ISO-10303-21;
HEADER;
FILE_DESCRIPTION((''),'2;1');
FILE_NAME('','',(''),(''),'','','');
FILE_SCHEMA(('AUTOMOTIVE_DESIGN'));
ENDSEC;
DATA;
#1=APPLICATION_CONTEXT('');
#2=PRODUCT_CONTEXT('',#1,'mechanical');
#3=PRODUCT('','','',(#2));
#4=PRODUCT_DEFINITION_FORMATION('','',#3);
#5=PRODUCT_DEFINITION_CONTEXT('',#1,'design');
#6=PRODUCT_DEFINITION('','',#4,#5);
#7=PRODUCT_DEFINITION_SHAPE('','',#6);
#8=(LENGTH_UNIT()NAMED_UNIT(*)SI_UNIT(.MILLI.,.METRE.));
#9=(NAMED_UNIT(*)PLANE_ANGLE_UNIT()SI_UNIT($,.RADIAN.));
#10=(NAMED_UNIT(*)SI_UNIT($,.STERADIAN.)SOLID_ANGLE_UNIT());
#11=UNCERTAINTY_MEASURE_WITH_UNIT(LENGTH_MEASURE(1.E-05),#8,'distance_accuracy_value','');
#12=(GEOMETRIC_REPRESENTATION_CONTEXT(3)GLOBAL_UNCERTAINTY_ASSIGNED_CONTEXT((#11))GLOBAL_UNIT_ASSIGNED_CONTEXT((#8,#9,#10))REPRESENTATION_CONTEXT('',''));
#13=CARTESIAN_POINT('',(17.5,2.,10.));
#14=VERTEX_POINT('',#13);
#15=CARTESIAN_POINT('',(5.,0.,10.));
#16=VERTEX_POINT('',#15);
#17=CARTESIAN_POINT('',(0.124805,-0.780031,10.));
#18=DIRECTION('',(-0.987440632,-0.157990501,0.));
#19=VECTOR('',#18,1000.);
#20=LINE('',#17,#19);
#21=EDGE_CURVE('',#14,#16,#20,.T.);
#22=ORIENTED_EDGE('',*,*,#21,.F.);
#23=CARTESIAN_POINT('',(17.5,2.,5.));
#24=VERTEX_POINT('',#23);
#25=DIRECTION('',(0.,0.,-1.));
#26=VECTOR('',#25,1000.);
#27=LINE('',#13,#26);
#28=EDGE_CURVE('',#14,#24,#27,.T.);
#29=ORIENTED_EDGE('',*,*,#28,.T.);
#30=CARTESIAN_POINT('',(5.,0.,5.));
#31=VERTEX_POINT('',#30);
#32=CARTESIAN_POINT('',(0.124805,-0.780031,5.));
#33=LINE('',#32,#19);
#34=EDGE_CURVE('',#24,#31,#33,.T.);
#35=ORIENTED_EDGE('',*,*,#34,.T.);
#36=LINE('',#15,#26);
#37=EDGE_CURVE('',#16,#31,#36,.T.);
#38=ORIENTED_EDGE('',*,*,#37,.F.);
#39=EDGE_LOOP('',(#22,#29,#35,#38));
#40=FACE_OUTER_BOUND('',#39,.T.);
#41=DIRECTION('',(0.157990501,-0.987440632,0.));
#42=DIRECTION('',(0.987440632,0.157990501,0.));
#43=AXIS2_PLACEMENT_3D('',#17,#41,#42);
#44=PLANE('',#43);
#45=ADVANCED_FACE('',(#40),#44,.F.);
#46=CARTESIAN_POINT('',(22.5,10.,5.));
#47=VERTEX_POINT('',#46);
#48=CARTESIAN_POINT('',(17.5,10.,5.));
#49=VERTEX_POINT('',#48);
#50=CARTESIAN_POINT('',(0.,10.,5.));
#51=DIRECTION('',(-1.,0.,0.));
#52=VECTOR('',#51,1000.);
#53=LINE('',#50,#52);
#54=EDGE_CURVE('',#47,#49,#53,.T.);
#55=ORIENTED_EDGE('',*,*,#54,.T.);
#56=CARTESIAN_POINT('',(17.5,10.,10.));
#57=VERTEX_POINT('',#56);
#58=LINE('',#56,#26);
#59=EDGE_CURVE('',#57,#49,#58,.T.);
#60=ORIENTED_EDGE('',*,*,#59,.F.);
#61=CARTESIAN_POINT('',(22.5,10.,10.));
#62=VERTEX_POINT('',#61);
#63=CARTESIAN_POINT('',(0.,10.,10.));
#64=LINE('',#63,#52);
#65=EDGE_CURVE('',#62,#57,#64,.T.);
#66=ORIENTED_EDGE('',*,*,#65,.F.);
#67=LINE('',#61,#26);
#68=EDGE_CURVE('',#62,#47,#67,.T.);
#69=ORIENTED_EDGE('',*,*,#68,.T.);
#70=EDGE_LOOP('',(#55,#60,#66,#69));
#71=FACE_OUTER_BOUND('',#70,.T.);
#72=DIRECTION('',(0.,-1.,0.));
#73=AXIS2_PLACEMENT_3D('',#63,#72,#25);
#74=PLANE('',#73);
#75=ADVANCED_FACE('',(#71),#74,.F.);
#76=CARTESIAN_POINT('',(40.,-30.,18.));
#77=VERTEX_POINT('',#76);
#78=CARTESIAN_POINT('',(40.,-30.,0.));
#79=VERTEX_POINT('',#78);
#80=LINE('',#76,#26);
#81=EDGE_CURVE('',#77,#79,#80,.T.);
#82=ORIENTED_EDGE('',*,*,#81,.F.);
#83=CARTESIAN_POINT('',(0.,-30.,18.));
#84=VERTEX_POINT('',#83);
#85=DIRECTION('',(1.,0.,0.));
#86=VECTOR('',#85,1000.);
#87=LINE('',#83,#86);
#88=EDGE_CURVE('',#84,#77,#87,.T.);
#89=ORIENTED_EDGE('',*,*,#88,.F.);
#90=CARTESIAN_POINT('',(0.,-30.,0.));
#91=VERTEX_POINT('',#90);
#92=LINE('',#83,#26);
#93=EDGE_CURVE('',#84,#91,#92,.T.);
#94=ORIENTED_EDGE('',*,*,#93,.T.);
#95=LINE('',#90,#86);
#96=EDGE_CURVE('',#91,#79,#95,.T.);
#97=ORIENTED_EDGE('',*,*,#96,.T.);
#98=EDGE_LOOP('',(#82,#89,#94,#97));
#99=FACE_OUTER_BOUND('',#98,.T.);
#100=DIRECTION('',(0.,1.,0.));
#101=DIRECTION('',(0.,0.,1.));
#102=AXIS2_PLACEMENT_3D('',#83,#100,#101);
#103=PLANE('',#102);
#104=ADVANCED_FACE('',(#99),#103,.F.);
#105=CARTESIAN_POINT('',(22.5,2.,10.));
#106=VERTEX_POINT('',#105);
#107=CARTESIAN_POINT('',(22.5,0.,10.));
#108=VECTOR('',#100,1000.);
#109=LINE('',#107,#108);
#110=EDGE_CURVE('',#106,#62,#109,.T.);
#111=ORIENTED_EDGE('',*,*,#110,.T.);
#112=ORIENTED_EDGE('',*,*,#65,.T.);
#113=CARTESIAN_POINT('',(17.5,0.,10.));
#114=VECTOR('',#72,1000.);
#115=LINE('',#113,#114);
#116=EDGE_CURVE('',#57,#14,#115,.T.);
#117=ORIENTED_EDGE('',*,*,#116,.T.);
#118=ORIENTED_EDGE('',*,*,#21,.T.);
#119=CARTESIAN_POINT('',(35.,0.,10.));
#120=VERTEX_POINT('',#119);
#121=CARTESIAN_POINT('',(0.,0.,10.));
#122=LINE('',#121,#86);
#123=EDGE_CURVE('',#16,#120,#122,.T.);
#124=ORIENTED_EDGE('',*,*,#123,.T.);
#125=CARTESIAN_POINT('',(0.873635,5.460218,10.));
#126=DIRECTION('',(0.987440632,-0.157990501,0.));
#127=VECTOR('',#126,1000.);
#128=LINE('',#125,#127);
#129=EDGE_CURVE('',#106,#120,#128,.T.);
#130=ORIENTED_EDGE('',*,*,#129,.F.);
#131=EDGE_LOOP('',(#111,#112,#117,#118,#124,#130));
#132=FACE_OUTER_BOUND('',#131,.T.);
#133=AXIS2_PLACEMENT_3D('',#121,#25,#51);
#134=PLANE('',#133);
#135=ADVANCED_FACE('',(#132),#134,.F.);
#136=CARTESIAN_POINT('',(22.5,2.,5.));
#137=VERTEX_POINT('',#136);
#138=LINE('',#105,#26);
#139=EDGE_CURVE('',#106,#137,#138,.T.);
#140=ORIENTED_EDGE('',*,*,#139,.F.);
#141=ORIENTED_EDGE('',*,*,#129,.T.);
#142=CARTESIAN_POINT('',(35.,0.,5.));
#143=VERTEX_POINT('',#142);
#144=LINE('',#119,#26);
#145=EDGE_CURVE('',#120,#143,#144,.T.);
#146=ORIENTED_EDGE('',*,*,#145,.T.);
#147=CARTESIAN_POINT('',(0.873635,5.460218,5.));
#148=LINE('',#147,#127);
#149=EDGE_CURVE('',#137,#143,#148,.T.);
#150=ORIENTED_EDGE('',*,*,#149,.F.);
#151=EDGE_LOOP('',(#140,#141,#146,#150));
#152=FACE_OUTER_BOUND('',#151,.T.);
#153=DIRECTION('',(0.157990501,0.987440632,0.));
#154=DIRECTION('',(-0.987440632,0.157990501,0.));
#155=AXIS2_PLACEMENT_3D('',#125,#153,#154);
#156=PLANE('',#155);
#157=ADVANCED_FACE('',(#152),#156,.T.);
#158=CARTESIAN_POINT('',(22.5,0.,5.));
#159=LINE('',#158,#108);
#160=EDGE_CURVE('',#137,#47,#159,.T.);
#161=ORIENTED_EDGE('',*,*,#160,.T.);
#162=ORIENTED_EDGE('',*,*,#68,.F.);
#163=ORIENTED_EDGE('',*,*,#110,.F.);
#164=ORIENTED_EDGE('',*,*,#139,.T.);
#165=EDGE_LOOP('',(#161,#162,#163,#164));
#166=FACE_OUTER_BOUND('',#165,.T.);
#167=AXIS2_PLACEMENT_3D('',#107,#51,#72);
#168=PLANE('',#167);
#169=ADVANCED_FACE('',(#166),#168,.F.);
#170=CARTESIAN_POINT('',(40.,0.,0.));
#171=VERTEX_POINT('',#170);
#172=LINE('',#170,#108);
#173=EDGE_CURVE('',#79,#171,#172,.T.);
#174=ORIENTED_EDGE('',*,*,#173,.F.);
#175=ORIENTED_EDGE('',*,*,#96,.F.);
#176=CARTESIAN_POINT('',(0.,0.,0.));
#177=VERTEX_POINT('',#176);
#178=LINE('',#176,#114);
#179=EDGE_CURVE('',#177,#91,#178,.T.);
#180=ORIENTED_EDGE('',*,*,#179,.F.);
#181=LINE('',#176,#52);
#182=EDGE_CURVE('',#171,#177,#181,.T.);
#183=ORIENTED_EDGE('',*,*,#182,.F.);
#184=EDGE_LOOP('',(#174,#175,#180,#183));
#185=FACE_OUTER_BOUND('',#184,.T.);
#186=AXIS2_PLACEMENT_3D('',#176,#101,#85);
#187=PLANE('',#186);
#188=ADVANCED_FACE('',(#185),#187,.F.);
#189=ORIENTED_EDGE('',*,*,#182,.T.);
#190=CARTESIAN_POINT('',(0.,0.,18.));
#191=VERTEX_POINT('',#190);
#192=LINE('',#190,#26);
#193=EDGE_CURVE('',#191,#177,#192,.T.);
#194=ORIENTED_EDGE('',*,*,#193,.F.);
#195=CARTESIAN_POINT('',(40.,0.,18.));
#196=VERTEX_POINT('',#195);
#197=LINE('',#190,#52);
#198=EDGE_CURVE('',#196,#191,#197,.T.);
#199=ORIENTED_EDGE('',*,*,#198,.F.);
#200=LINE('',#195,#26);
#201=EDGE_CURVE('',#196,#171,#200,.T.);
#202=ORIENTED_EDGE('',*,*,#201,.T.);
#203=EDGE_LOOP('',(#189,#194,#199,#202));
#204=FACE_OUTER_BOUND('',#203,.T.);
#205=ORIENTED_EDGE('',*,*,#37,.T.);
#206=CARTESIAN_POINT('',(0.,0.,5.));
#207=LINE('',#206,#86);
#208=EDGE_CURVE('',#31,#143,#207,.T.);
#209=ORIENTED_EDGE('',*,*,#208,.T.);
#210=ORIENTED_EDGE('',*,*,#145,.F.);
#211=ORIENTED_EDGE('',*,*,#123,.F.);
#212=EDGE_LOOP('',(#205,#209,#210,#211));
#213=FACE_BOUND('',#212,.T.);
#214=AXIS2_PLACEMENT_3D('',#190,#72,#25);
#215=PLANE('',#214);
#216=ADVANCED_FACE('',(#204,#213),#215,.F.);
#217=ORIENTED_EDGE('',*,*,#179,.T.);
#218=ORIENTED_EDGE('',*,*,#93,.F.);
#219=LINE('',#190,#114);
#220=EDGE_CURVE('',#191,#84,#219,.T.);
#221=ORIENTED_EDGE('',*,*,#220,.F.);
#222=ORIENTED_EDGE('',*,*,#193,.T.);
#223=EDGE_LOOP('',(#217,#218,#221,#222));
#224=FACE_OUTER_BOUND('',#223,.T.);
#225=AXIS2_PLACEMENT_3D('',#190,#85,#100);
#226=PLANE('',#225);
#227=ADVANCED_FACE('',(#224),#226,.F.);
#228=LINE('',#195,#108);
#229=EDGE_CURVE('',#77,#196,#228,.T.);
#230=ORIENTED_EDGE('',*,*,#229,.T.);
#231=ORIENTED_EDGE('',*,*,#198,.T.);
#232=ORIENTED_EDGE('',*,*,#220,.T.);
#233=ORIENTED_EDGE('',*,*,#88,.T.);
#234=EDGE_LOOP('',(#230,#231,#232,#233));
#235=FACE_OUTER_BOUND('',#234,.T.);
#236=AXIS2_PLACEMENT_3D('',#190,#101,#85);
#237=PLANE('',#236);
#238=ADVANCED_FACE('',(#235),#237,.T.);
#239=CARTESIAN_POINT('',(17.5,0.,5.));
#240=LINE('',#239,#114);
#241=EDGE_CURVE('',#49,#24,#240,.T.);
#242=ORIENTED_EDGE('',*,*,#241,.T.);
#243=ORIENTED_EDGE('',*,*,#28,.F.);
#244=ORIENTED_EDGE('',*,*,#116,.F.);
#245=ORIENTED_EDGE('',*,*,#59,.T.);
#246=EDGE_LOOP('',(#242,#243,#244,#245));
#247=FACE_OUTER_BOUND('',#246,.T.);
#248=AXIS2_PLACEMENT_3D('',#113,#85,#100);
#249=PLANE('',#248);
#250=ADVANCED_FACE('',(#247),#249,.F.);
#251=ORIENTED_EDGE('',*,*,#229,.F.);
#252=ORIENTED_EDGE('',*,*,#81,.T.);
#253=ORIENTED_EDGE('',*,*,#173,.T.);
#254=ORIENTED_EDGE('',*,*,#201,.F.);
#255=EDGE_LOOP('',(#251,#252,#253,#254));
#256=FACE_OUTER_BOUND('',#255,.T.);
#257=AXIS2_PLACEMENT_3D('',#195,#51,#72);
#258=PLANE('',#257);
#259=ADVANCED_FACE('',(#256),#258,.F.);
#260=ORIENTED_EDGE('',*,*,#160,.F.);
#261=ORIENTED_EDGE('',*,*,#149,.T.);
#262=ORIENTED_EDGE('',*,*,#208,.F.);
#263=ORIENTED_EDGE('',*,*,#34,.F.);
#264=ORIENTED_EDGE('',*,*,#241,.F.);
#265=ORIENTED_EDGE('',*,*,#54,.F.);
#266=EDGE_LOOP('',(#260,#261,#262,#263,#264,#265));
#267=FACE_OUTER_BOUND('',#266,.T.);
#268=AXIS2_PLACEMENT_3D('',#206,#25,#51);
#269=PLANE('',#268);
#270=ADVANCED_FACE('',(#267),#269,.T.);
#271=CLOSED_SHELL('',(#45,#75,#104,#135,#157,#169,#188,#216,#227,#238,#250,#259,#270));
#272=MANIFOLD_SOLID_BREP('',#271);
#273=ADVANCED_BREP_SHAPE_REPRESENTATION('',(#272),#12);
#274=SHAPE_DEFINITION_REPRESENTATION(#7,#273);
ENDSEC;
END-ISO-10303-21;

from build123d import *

# Parameters (mm, degrees)
SKETCH1_W           = 40
SKETCH1_H           = 30
BOSS_EXTRUDE1_DEPTH = 18
BOSS_EXTRUDE3_START = 5
BOSS_EXTRUDE3_DEPTH = 5


with BuildPart() as part:
    # Sketch1 → Boss-Extrude1 (new body)
    with BuildSketch(Plane.XY):
        with Locations((20, -15)):
            Rectangle(SKETCH1_W, SKETCH1_H)
    extrude(amount=BOSS_EXTRUDE1_DEPTH)

    # Sketch2 → Boss-Extrude3 (add)
    with BuildSketch(Plane.XY.offset(BOSS_EXTRUDE3_START)):
        Polygon((17.5, 10), (17.5, 2), (5, 0), (35, 0), (22.5, 2), (22.5, 10), align=None)
    extrude(amount=BOSS_EXTRUDE3_DEPTH)


solid = part.part
